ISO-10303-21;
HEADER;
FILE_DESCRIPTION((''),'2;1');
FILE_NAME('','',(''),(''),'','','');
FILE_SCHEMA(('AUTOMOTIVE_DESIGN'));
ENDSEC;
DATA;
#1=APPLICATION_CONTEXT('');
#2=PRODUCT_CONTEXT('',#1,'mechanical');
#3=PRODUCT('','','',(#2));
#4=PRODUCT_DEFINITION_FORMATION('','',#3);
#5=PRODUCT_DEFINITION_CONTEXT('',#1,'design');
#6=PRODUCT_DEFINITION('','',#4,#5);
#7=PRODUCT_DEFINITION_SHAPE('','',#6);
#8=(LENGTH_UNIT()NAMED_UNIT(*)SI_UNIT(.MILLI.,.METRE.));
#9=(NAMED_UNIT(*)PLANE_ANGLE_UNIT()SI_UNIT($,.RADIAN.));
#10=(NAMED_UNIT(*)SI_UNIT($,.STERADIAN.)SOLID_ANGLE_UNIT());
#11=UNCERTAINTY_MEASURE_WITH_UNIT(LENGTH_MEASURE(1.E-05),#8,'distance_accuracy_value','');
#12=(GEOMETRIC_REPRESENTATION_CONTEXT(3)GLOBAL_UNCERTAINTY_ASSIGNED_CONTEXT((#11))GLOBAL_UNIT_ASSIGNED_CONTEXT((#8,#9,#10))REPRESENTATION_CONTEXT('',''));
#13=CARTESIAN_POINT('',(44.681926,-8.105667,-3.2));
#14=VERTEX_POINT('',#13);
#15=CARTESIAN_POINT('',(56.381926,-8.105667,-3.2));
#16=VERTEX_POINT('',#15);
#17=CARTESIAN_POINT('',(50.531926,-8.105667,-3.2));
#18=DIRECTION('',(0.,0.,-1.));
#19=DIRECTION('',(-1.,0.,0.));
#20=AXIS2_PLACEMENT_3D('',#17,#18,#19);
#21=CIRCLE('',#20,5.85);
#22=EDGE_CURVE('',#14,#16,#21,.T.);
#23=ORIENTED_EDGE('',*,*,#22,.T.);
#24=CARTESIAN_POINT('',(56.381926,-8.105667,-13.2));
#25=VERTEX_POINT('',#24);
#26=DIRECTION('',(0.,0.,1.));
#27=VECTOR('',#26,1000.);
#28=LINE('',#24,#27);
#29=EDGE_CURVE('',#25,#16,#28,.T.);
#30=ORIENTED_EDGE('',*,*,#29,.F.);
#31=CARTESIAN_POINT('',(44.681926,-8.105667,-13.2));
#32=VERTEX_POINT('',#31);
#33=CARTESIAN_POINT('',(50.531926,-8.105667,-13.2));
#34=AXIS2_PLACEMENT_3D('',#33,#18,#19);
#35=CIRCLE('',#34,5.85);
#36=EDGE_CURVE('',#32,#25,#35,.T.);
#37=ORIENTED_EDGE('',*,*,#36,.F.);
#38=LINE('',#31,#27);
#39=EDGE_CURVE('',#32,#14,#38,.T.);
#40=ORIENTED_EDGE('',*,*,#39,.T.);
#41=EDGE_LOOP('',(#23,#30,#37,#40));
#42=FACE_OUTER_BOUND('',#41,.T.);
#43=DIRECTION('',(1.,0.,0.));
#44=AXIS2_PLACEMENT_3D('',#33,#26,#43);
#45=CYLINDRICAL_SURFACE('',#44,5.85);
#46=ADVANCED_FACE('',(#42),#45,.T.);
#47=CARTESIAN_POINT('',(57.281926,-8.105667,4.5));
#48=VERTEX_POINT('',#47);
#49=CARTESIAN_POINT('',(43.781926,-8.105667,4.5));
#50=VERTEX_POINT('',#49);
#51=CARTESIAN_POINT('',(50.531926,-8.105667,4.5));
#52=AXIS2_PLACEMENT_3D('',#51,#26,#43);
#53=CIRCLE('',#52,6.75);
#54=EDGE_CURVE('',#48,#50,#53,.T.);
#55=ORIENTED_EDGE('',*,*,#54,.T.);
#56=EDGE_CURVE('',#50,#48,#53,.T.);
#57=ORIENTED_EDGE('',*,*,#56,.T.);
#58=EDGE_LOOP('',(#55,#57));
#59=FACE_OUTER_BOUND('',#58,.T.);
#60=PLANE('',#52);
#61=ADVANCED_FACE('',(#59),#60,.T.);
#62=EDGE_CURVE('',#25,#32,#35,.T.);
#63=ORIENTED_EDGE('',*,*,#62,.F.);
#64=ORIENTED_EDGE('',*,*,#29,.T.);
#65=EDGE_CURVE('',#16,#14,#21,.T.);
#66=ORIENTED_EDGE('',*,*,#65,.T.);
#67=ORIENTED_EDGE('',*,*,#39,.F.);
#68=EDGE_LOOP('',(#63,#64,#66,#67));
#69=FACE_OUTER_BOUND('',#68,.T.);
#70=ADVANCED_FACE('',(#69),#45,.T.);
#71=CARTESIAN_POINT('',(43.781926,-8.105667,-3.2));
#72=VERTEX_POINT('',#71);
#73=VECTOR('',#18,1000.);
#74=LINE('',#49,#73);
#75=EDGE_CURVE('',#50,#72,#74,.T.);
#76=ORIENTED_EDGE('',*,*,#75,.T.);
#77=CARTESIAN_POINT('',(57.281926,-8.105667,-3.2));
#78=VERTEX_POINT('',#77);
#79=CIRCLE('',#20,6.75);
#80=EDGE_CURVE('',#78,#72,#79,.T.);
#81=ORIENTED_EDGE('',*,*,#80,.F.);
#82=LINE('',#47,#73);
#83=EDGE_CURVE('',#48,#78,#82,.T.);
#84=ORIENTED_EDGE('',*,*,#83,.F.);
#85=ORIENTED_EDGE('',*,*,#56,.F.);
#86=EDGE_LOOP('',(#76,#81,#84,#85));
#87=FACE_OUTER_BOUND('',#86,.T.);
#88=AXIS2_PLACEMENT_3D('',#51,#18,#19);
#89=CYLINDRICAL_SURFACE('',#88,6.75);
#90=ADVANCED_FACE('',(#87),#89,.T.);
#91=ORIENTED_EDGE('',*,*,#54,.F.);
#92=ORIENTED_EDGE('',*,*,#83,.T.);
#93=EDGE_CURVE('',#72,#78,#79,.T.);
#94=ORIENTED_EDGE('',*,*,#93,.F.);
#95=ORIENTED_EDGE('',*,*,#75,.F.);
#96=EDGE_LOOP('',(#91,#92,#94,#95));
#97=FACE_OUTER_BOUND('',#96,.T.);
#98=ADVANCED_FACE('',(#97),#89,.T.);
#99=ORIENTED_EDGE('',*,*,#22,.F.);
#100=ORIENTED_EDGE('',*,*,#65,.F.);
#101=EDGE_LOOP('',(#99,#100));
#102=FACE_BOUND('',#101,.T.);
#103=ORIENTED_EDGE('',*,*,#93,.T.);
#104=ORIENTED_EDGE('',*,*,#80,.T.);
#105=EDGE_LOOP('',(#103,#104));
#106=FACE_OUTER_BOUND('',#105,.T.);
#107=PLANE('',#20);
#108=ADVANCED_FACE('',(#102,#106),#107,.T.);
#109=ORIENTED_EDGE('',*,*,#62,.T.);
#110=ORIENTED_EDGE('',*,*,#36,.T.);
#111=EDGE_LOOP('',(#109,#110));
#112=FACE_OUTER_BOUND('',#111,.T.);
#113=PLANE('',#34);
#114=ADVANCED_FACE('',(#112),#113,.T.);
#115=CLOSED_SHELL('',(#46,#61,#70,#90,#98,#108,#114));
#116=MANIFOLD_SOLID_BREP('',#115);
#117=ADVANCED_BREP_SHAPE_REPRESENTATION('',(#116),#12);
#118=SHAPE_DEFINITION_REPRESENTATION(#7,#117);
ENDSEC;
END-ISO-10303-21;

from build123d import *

# Parameters (mm, degrees)
SKETCH1_R           = 6.75
BOSS_EXTRUDE1_DEPTH = 4.5
BOSS_EXTRUDE2_START = 3.2
SKETCH2_R           = 6.75
BOSS_EXTRUDE2_DEPTH = 3.2
SKETCH3_R           = 5.85
BOSS_EXTRUDE3_DEPTH = 10


with BuildPart() as part:
    # Sketch1 → Boss-Extrude1 (new body)
    with BuildSketch(Plane.XY):
        with Locations((50.531925728, -8.105666666)):
            Circle(SKETCH1_R)
    extrude(amount=BOSS_EXTRUDE1_DEPTH)

    # Sketch2 → Boss-Extrude2 (add)
    with BuildSketch(Plane(origin=(0, 0, 0), x_dir=(-1, 0, 0), z_dir=(0, 0, -1)).offset(BOSS_EXTRUDE2_START)):
        with Locations((-50.531925728, -8.105666666)):
            Circle(SKETCH2_R)
    extrude(amount=-BOSS_EXTRUDE2_DEPTH)

    # Sketch3 → Boss-Extrude3 (add)
    with BuildSketch(Plane(origin=(0, 0, -3.2), x_dir=(-1, 0, 0), z_dir=(0, 0, -1))):
        with Locations((-50.531925728, -8.105666666)):
            Circle(SKETCH3_R)
    extrude(amount=BOSS_EXTRUDE3_DEPTH)


solid = part.part
